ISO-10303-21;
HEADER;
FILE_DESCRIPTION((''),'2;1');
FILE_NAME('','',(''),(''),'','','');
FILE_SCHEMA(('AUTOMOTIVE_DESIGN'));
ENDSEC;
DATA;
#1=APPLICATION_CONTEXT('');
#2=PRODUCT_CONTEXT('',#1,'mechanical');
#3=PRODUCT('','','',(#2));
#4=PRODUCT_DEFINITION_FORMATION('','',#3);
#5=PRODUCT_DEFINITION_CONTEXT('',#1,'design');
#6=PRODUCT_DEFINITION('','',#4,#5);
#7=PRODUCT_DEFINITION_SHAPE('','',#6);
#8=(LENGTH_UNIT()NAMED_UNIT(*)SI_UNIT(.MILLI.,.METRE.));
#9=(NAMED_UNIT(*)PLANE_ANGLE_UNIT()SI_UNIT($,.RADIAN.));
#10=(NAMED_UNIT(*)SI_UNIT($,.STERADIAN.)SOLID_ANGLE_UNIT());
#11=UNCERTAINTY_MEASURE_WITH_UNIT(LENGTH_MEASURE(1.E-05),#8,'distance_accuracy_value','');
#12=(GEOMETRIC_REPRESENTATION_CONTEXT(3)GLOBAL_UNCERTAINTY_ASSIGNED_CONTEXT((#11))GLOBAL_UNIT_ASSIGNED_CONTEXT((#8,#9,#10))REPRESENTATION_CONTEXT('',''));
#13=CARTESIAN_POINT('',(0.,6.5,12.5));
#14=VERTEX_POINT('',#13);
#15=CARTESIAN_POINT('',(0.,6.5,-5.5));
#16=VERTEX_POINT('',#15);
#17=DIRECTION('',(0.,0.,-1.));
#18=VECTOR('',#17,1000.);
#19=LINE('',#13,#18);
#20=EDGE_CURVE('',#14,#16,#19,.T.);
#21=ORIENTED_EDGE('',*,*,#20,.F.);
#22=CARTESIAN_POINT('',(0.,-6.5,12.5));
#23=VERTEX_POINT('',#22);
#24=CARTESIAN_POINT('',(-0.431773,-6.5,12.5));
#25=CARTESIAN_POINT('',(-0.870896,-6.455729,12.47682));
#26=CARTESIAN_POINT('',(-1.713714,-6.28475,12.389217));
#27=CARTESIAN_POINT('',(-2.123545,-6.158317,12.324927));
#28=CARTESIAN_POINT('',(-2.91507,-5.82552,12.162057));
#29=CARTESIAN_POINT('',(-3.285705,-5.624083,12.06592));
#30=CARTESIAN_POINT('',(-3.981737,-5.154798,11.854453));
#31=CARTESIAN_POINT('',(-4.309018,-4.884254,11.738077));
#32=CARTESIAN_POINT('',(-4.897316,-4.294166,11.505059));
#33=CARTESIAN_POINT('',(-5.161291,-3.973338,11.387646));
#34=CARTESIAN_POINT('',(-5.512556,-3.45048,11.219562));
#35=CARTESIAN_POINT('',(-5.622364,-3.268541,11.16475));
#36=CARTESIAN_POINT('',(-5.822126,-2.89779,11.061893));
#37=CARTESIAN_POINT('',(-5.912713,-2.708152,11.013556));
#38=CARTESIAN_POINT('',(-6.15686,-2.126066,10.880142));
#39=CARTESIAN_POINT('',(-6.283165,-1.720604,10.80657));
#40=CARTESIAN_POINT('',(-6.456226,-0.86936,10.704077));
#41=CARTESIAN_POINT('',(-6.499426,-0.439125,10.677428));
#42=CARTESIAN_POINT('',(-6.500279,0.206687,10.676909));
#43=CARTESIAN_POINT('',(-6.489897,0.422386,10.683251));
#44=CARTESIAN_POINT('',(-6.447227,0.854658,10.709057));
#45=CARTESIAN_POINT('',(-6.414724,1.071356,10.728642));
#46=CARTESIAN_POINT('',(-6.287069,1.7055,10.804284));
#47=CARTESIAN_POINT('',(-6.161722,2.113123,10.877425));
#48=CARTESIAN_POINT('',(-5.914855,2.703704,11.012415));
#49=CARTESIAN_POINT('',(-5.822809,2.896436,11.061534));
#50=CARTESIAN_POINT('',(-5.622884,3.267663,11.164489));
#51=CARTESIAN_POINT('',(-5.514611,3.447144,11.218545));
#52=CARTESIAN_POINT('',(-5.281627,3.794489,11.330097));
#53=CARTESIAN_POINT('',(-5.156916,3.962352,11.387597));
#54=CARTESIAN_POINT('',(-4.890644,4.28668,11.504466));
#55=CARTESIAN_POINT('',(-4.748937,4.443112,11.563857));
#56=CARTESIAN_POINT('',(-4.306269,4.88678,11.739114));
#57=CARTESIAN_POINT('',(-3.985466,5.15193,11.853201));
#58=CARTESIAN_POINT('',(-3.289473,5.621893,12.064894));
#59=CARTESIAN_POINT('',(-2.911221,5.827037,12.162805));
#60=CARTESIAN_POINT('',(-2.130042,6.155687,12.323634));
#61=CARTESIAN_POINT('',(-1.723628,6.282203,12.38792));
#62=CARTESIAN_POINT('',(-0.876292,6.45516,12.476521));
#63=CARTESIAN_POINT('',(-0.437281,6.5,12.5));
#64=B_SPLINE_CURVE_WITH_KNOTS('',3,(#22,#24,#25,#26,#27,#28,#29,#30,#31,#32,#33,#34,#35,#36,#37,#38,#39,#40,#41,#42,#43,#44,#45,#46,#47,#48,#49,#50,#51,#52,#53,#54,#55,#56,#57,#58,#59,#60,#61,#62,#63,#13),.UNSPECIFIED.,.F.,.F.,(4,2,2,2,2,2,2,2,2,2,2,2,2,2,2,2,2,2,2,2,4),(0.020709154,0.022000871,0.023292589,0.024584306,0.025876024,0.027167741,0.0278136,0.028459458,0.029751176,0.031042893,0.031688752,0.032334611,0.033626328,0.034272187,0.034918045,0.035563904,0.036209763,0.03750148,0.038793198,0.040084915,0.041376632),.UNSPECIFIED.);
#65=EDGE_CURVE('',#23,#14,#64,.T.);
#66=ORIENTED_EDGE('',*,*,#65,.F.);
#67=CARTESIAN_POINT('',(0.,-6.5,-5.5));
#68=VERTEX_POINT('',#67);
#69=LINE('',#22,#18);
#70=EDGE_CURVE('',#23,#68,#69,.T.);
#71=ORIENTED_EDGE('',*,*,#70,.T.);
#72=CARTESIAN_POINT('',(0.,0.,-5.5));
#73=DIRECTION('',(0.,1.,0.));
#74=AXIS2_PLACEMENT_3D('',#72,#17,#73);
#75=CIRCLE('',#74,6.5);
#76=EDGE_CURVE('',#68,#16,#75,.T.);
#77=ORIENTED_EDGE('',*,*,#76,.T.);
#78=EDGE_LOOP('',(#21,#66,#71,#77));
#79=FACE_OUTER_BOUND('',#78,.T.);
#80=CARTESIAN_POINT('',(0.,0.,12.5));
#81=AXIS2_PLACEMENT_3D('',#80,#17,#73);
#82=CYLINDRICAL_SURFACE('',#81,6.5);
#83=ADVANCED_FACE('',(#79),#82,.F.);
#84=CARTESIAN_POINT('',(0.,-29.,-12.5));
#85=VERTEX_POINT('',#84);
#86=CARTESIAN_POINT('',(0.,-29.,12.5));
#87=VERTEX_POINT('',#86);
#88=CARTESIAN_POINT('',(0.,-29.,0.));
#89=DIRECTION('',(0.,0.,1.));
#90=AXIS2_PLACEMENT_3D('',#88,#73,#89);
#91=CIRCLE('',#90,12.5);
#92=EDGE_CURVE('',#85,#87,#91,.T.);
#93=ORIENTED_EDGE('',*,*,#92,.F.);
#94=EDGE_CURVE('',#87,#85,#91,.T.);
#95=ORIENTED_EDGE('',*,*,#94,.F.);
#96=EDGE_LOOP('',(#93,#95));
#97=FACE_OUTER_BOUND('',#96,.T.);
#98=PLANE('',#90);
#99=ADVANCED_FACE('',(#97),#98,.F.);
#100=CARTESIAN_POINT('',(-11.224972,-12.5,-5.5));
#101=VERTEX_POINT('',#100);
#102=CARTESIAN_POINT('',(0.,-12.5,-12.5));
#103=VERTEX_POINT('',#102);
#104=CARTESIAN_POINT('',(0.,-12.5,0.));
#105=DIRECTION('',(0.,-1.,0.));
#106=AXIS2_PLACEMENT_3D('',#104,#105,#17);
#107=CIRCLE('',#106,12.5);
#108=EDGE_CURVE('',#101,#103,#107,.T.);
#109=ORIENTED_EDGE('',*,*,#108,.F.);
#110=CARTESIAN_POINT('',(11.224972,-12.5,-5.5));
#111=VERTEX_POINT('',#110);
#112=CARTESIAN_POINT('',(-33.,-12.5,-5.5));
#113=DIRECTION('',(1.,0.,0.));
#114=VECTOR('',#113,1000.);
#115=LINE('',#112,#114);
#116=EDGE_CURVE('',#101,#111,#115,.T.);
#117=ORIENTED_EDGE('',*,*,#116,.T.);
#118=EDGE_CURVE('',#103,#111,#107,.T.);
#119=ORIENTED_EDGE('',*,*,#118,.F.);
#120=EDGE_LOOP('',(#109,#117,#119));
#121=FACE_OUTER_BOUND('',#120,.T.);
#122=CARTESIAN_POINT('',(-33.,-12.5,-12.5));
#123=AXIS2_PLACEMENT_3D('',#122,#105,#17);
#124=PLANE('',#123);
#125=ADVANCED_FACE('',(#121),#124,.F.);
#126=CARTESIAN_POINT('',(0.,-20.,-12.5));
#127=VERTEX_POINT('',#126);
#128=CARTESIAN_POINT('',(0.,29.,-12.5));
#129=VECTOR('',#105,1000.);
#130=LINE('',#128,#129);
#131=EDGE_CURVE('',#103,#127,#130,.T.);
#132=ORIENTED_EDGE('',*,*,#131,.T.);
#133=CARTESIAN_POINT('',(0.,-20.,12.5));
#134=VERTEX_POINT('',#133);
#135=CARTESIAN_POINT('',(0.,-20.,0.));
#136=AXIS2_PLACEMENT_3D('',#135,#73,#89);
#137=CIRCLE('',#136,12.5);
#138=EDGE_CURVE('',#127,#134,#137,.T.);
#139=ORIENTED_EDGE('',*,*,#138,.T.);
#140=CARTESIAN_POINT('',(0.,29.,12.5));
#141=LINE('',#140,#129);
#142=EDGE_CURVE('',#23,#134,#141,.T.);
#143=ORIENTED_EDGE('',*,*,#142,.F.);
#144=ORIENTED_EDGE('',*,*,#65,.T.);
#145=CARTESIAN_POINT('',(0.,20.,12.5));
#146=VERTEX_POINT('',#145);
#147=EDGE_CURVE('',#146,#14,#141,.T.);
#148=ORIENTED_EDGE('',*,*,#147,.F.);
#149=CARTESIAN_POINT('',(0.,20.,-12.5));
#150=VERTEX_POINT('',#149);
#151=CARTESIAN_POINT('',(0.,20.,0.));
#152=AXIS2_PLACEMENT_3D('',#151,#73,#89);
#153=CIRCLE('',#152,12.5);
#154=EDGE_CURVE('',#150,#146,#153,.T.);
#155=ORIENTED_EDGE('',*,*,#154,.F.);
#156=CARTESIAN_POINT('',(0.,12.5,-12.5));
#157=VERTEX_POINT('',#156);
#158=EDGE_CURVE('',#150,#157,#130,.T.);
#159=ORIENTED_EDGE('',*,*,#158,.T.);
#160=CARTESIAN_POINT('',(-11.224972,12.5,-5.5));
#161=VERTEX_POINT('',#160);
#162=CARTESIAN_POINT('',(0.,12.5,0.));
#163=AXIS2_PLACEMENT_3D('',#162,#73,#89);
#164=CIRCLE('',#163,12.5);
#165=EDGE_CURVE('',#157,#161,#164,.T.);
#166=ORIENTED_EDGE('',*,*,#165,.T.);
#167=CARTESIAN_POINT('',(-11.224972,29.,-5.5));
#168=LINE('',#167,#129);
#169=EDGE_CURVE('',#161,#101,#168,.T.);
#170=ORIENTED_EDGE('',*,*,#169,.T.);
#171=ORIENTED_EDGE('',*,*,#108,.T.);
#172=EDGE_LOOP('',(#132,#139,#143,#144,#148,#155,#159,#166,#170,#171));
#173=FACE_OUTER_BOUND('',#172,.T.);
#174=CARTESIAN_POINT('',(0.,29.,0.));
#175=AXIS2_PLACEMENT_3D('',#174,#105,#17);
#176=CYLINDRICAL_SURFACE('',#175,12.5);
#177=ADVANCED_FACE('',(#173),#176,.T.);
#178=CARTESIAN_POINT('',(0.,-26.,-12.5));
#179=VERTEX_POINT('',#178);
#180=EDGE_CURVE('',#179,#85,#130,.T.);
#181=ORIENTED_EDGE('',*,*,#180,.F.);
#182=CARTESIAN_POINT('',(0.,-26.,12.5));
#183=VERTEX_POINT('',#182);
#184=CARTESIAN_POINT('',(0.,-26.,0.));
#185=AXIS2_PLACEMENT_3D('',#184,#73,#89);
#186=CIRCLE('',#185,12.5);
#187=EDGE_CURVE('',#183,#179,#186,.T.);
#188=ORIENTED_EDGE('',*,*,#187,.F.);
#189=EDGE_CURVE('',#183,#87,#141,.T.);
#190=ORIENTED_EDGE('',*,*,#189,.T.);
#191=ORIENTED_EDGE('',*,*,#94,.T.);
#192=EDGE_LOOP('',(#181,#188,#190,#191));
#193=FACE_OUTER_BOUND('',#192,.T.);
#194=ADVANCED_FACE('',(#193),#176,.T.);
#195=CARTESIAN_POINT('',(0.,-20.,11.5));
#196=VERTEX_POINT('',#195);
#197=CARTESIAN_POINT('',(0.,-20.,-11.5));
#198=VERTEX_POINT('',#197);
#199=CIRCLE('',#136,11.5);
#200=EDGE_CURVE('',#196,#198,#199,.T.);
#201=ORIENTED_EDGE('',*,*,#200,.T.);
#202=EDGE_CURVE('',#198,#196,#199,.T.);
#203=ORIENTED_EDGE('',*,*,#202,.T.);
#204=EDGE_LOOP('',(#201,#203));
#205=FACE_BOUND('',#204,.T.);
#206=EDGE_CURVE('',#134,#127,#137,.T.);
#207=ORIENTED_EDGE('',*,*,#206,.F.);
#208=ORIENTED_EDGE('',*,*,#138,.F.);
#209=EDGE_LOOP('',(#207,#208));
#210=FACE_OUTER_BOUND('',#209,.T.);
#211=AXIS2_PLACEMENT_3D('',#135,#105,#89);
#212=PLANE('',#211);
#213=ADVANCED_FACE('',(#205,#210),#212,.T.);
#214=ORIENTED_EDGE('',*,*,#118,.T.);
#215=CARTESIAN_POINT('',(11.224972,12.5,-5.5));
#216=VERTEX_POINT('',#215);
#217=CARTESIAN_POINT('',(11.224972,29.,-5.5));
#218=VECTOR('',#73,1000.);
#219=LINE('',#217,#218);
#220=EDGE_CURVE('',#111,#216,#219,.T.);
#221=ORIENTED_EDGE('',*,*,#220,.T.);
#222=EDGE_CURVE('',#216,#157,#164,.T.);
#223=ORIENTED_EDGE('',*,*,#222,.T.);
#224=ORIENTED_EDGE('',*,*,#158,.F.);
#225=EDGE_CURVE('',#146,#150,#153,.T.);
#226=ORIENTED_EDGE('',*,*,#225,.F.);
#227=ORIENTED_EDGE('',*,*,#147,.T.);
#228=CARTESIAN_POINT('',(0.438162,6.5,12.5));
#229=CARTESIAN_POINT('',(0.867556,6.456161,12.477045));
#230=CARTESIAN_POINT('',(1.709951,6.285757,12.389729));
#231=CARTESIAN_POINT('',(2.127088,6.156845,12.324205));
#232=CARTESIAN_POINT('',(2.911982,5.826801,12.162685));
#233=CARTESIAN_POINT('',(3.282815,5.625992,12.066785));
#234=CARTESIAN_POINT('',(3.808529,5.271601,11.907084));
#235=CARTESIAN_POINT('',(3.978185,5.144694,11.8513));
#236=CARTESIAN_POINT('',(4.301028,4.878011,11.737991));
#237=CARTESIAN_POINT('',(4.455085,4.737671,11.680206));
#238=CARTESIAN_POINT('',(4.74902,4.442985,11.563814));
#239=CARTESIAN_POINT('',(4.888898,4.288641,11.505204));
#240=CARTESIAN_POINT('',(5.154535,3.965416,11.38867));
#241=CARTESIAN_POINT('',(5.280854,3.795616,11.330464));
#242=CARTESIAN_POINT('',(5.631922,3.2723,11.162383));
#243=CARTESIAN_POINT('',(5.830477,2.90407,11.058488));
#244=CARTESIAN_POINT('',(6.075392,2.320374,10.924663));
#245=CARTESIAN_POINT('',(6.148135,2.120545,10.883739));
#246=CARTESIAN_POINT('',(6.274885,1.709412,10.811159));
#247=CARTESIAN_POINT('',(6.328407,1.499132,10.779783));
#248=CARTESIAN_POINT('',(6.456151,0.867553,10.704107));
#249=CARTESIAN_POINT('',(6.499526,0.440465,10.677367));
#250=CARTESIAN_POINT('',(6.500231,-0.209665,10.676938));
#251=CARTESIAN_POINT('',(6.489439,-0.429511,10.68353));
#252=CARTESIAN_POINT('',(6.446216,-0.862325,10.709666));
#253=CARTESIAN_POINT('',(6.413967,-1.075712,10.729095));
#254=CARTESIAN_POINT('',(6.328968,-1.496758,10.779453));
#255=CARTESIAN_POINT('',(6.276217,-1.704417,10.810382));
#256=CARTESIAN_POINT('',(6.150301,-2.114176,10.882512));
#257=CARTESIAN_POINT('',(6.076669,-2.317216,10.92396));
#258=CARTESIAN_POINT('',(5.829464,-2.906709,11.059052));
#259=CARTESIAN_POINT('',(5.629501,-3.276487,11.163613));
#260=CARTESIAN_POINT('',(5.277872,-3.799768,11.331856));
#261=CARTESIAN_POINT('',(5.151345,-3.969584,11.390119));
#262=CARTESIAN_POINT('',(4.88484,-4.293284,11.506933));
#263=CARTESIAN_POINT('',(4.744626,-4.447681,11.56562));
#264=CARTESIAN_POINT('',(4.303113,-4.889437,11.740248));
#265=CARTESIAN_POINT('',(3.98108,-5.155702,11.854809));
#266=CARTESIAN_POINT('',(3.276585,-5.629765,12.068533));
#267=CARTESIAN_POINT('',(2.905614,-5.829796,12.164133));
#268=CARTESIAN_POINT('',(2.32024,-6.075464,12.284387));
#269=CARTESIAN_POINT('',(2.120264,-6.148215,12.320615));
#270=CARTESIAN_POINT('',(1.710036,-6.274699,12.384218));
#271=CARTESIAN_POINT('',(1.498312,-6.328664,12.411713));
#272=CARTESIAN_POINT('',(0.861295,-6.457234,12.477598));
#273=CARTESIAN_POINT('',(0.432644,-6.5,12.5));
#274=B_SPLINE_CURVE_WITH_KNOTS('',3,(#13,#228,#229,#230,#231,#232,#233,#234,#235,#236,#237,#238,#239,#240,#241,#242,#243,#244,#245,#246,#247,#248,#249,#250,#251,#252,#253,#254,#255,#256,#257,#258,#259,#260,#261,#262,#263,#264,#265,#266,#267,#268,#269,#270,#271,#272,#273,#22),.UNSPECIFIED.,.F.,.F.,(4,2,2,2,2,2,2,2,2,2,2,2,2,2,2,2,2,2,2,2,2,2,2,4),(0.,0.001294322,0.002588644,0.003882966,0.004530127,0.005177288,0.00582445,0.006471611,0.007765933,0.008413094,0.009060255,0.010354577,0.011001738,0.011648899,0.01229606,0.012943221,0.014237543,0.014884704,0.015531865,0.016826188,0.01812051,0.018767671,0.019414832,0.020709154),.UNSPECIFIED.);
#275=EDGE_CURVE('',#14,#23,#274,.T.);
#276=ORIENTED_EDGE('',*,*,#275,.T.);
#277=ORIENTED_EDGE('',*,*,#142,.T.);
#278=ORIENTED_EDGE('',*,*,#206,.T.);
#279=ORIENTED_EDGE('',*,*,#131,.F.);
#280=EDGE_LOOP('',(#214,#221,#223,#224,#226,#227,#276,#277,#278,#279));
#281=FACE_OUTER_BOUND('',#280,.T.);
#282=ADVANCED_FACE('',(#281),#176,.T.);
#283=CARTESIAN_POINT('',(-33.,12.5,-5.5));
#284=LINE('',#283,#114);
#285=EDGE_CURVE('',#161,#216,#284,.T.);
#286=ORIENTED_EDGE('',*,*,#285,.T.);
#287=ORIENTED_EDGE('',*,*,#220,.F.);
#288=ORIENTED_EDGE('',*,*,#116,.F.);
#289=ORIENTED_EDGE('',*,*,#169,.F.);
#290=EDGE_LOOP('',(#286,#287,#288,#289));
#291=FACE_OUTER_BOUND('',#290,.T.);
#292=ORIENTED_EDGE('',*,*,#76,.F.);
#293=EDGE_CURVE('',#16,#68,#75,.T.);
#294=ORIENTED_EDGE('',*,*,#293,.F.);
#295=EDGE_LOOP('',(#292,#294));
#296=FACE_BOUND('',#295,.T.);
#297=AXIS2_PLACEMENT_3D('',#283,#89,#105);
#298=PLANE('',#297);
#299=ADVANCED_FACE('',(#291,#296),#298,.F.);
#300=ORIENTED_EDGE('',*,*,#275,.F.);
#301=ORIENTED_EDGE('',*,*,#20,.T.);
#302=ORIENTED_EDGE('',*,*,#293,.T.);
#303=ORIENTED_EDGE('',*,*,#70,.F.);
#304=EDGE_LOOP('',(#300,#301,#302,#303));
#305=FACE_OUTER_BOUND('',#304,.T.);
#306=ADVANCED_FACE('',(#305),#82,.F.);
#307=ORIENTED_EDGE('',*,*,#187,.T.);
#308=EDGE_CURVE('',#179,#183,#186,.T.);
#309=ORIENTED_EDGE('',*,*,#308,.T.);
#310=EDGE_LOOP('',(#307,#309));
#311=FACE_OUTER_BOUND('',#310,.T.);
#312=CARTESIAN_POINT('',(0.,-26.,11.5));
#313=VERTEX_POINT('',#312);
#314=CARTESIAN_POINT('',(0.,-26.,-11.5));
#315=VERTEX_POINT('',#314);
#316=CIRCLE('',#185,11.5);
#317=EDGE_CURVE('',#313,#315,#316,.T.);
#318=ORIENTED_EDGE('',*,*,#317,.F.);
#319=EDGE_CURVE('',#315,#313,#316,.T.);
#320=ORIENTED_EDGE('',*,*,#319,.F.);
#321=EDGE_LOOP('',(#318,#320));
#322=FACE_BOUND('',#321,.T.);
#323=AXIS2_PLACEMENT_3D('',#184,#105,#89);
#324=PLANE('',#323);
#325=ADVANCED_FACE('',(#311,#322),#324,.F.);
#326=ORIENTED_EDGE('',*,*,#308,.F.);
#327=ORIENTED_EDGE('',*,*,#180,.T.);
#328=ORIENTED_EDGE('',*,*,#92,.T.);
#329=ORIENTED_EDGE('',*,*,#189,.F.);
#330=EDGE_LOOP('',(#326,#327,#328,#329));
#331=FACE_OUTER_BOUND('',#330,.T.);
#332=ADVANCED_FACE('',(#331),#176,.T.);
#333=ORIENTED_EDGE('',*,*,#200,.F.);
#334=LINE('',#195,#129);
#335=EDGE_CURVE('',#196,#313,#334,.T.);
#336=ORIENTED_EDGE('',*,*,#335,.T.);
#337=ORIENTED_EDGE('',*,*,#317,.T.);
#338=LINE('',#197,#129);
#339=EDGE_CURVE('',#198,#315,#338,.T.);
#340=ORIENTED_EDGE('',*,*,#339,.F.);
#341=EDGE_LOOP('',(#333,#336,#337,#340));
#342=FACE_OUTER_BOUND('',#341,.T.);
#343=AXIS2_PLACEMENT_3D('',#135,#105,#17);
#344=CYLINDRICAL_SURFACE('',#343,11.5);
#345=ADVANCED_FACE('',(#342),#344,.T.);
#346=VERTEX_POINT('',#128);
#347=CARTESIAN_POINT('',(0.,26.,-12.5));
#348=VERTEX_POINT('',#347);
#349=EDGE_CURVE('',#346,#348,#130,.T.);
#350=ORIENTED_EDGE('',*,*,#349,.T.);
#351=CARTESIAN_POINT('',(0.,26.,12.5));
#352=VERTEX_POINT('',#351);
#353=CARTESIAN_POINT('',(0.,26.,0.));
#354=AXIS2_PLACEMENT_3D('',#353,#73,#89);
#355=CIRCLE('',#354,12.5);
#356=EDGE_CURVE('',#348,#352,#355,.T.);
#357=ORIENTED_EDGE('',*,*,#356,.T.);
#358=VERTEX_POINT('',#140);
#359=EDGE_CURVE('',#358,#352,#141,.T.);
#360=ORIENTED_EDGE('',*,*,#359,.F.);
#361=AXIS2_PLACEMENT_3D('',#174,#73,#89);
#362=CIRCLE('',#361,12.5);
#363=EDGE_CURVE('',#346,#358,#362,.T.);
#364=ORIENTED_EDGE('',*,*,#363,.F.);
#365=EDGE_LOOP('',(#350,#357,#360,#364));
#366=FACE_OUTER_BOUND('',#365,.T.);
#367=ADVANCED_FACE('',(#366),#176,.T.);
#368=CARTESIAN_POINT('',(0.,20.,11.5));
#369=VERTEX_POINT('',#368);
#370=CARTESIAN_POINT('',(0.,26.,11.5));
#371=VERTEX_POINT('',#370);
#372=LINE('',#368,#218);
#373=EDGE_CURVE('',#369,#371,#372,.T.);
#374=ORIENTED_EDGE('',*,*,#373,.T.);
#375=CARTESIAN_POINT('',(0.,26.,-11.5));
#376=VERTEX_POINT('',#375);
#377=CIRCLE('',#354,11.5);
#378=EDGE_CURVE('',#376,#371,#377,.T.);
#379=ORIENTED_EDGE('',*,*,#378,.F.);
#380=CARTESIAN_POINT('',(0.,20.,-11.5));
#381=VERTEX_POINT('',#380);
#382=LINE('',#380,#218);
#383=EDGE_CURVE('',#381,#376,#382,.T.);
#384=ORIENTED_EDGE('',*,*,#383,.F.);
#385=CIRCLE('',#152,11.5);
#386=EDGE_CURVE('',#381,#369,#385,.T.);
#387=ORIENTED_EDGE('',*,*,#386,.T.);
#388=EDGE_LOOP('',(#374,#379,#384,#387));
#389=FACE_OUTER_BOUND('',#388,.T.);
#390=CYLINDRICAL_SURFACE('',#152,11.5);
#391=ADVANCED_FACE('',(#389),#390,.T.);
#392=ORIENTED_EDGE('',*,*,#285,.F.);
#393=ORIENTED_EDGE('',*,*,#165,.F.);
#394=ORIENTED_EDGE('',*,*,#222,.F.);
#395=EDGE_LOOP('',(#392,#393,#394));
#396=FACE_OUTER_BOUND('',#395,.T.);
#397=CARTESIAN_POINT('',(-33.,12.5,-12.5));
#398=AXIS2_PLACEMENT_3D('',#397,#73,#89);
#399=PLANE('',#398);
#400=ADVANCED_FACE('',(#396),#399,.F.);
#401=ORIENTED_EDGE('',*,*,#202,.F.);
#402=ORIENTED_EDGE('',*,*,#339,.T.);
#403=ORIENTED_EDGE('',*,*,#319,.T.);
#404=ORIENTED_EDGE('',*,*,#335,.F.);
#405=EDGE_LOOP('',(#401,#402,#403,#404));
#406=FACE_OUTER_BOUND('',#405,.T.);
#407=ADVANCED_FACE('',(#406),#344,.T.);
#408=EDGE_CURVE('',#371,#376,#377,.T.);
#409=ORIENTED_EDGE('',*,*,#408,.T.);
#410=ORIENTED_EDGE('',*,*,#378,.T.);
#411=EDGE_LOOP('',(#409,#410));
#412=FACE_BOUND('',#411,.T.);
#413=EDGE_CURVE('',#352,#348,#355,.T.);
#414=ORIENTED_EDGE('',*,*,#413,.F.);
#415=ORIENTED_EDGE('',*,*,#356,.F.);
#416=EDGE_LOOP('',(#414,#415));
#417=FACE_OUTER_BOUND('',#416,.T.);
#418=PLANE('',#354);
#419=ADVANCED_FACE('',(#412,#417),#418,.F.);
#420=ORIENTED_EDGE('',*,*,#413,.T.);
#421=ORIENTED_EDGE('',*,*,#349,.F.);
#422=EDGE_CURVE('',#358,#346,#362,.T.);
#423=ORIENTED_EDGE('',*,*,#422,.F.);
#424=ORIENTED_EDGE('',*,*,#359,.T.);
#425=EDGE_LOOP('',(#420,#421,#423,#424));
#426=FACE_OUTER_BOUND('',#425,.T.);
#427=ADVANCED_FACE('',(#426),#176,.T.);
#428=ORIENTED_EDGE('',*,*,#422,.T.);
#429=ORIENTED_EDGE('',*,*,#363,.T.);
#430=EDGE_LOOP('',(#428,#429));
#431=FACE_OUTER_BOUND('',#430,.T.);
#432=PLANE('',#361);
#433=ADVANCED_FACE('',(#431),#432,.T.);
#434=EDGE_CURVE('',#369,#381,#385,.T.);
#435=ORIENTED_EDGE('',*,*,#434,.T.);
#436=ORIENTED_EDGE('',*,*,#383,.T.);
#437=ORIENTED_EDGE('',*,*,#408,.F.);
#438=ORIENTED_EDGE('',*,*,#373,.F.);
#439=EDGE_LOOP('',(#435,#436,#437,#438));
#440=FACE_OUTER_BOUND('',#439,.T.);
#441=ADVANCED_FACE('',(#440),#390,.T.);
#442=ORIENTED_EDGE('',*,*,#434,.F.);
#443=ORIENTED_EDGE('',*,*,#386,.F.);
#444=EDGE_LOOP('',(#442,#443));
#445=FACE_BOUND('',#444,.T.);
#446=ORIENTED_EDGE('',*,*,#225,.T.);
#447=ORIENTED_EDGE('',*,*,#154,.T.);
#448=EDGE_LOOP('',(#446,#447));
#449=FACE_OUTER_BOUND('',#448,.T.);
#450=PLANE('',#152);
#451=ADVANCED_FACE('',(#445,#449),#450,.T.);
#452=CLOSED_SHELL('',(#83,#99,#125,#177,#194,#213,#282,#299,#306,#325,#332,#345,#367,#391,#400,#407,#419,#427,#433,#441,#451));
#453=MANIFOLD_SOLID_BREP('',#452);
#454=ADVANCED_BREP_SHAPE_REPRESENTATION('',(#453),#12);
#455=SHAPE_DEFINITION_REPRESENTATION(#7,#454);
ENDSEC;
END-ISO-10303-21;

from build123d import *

# Parameters (mm, degrees)
SKETCH1_R           = 12.5
BOSS_EXTRUDE1_DEPTH = 29
CUT_EXTRUDE1_START  = -3
SKETCH2_R           = 12.5
SKETCH2_R_2         = 11.5
CUT_EXTRUDE1_DEPTH  = 6
SKETCH3_W           = 7
SKETCH3_H           = 25
CUT_EXTRUDE2_DEPTH  = 33
SKETCH4_R           = 6.5
CUT_EXTRUDE3_DEPTH  = 37.349002737


with BuildPart() as part:
    # Sketch1 → Boss-Extrude1 (new, symmetric)
    with BuildSketch(Plane(origin=(0, 0, 0), x_dir=(1, 0, 0), z_dir=(0, 1, 0))):
        with Locations(Location((0, 0, 0), (0, 0, 90))):
            Circle(SKETCH1_R)
    extrude(amount=BOSS_EXTRUDE1_DEPTH, both=True)

    # Sketch2 → Cut-Extrude1 (cut)
    with BuildSketch(Plane(origin=(0, 29, 0), x_dir=(1, 0, 0), z_dir=(0, 1, 0)).offset(CUT_EXTRUDE1_START)):
        with Locations(Location((0, 0, 0), (0, 0, 90))):
            Circle(SKETCH2_R)
        with Locations(Location((0, 0, 0), (0, 0, 270))):
            Circle(SKETCH2_R_2, mode=Mode.SUBTRACT)
    cut_extrude1 = extrude(amount=-CUT_EXTRUDE1_DEPTH, mode=Mode.SUBTRACT)

    # Mirror1: Cut-Extrude1 across plane
    add(cut_extrude1.mirror(Plane.ZX), mode=Mode.SUBTRACT)

    # Sketch3 → Cut-Extrude2 (cut, symmetric)
    with BuildSketch(Plane(origin=(0, 0, 0), x_dir=(0, 0, -1), z_dir=(1, 0, 0))):
        with Locations((9, 0)):
            Rectangle(SKETCH3_W, SKETCH3_H)
    extrude(amount=CUT_EXTRUDE2_DEPTH, both=True, mode=Mode.SUBTRACT)

    # Sketch4 → Cut-Extrude3 (cut, through all)
    with BuildSketch(Plane(origin=(0, 0, -5.5), x_dir=(-1, 0, 0), z_dir=(0, 0, -1))):
        with Locations(Location((0, 0, 0), (0, 0, 90))):
            Circle(SKETCH4_R)
    extrude(amount=-CUT_EXTRUDE3_DEPTH, mode=Mode.SUBTRACT)


solid = part.part
